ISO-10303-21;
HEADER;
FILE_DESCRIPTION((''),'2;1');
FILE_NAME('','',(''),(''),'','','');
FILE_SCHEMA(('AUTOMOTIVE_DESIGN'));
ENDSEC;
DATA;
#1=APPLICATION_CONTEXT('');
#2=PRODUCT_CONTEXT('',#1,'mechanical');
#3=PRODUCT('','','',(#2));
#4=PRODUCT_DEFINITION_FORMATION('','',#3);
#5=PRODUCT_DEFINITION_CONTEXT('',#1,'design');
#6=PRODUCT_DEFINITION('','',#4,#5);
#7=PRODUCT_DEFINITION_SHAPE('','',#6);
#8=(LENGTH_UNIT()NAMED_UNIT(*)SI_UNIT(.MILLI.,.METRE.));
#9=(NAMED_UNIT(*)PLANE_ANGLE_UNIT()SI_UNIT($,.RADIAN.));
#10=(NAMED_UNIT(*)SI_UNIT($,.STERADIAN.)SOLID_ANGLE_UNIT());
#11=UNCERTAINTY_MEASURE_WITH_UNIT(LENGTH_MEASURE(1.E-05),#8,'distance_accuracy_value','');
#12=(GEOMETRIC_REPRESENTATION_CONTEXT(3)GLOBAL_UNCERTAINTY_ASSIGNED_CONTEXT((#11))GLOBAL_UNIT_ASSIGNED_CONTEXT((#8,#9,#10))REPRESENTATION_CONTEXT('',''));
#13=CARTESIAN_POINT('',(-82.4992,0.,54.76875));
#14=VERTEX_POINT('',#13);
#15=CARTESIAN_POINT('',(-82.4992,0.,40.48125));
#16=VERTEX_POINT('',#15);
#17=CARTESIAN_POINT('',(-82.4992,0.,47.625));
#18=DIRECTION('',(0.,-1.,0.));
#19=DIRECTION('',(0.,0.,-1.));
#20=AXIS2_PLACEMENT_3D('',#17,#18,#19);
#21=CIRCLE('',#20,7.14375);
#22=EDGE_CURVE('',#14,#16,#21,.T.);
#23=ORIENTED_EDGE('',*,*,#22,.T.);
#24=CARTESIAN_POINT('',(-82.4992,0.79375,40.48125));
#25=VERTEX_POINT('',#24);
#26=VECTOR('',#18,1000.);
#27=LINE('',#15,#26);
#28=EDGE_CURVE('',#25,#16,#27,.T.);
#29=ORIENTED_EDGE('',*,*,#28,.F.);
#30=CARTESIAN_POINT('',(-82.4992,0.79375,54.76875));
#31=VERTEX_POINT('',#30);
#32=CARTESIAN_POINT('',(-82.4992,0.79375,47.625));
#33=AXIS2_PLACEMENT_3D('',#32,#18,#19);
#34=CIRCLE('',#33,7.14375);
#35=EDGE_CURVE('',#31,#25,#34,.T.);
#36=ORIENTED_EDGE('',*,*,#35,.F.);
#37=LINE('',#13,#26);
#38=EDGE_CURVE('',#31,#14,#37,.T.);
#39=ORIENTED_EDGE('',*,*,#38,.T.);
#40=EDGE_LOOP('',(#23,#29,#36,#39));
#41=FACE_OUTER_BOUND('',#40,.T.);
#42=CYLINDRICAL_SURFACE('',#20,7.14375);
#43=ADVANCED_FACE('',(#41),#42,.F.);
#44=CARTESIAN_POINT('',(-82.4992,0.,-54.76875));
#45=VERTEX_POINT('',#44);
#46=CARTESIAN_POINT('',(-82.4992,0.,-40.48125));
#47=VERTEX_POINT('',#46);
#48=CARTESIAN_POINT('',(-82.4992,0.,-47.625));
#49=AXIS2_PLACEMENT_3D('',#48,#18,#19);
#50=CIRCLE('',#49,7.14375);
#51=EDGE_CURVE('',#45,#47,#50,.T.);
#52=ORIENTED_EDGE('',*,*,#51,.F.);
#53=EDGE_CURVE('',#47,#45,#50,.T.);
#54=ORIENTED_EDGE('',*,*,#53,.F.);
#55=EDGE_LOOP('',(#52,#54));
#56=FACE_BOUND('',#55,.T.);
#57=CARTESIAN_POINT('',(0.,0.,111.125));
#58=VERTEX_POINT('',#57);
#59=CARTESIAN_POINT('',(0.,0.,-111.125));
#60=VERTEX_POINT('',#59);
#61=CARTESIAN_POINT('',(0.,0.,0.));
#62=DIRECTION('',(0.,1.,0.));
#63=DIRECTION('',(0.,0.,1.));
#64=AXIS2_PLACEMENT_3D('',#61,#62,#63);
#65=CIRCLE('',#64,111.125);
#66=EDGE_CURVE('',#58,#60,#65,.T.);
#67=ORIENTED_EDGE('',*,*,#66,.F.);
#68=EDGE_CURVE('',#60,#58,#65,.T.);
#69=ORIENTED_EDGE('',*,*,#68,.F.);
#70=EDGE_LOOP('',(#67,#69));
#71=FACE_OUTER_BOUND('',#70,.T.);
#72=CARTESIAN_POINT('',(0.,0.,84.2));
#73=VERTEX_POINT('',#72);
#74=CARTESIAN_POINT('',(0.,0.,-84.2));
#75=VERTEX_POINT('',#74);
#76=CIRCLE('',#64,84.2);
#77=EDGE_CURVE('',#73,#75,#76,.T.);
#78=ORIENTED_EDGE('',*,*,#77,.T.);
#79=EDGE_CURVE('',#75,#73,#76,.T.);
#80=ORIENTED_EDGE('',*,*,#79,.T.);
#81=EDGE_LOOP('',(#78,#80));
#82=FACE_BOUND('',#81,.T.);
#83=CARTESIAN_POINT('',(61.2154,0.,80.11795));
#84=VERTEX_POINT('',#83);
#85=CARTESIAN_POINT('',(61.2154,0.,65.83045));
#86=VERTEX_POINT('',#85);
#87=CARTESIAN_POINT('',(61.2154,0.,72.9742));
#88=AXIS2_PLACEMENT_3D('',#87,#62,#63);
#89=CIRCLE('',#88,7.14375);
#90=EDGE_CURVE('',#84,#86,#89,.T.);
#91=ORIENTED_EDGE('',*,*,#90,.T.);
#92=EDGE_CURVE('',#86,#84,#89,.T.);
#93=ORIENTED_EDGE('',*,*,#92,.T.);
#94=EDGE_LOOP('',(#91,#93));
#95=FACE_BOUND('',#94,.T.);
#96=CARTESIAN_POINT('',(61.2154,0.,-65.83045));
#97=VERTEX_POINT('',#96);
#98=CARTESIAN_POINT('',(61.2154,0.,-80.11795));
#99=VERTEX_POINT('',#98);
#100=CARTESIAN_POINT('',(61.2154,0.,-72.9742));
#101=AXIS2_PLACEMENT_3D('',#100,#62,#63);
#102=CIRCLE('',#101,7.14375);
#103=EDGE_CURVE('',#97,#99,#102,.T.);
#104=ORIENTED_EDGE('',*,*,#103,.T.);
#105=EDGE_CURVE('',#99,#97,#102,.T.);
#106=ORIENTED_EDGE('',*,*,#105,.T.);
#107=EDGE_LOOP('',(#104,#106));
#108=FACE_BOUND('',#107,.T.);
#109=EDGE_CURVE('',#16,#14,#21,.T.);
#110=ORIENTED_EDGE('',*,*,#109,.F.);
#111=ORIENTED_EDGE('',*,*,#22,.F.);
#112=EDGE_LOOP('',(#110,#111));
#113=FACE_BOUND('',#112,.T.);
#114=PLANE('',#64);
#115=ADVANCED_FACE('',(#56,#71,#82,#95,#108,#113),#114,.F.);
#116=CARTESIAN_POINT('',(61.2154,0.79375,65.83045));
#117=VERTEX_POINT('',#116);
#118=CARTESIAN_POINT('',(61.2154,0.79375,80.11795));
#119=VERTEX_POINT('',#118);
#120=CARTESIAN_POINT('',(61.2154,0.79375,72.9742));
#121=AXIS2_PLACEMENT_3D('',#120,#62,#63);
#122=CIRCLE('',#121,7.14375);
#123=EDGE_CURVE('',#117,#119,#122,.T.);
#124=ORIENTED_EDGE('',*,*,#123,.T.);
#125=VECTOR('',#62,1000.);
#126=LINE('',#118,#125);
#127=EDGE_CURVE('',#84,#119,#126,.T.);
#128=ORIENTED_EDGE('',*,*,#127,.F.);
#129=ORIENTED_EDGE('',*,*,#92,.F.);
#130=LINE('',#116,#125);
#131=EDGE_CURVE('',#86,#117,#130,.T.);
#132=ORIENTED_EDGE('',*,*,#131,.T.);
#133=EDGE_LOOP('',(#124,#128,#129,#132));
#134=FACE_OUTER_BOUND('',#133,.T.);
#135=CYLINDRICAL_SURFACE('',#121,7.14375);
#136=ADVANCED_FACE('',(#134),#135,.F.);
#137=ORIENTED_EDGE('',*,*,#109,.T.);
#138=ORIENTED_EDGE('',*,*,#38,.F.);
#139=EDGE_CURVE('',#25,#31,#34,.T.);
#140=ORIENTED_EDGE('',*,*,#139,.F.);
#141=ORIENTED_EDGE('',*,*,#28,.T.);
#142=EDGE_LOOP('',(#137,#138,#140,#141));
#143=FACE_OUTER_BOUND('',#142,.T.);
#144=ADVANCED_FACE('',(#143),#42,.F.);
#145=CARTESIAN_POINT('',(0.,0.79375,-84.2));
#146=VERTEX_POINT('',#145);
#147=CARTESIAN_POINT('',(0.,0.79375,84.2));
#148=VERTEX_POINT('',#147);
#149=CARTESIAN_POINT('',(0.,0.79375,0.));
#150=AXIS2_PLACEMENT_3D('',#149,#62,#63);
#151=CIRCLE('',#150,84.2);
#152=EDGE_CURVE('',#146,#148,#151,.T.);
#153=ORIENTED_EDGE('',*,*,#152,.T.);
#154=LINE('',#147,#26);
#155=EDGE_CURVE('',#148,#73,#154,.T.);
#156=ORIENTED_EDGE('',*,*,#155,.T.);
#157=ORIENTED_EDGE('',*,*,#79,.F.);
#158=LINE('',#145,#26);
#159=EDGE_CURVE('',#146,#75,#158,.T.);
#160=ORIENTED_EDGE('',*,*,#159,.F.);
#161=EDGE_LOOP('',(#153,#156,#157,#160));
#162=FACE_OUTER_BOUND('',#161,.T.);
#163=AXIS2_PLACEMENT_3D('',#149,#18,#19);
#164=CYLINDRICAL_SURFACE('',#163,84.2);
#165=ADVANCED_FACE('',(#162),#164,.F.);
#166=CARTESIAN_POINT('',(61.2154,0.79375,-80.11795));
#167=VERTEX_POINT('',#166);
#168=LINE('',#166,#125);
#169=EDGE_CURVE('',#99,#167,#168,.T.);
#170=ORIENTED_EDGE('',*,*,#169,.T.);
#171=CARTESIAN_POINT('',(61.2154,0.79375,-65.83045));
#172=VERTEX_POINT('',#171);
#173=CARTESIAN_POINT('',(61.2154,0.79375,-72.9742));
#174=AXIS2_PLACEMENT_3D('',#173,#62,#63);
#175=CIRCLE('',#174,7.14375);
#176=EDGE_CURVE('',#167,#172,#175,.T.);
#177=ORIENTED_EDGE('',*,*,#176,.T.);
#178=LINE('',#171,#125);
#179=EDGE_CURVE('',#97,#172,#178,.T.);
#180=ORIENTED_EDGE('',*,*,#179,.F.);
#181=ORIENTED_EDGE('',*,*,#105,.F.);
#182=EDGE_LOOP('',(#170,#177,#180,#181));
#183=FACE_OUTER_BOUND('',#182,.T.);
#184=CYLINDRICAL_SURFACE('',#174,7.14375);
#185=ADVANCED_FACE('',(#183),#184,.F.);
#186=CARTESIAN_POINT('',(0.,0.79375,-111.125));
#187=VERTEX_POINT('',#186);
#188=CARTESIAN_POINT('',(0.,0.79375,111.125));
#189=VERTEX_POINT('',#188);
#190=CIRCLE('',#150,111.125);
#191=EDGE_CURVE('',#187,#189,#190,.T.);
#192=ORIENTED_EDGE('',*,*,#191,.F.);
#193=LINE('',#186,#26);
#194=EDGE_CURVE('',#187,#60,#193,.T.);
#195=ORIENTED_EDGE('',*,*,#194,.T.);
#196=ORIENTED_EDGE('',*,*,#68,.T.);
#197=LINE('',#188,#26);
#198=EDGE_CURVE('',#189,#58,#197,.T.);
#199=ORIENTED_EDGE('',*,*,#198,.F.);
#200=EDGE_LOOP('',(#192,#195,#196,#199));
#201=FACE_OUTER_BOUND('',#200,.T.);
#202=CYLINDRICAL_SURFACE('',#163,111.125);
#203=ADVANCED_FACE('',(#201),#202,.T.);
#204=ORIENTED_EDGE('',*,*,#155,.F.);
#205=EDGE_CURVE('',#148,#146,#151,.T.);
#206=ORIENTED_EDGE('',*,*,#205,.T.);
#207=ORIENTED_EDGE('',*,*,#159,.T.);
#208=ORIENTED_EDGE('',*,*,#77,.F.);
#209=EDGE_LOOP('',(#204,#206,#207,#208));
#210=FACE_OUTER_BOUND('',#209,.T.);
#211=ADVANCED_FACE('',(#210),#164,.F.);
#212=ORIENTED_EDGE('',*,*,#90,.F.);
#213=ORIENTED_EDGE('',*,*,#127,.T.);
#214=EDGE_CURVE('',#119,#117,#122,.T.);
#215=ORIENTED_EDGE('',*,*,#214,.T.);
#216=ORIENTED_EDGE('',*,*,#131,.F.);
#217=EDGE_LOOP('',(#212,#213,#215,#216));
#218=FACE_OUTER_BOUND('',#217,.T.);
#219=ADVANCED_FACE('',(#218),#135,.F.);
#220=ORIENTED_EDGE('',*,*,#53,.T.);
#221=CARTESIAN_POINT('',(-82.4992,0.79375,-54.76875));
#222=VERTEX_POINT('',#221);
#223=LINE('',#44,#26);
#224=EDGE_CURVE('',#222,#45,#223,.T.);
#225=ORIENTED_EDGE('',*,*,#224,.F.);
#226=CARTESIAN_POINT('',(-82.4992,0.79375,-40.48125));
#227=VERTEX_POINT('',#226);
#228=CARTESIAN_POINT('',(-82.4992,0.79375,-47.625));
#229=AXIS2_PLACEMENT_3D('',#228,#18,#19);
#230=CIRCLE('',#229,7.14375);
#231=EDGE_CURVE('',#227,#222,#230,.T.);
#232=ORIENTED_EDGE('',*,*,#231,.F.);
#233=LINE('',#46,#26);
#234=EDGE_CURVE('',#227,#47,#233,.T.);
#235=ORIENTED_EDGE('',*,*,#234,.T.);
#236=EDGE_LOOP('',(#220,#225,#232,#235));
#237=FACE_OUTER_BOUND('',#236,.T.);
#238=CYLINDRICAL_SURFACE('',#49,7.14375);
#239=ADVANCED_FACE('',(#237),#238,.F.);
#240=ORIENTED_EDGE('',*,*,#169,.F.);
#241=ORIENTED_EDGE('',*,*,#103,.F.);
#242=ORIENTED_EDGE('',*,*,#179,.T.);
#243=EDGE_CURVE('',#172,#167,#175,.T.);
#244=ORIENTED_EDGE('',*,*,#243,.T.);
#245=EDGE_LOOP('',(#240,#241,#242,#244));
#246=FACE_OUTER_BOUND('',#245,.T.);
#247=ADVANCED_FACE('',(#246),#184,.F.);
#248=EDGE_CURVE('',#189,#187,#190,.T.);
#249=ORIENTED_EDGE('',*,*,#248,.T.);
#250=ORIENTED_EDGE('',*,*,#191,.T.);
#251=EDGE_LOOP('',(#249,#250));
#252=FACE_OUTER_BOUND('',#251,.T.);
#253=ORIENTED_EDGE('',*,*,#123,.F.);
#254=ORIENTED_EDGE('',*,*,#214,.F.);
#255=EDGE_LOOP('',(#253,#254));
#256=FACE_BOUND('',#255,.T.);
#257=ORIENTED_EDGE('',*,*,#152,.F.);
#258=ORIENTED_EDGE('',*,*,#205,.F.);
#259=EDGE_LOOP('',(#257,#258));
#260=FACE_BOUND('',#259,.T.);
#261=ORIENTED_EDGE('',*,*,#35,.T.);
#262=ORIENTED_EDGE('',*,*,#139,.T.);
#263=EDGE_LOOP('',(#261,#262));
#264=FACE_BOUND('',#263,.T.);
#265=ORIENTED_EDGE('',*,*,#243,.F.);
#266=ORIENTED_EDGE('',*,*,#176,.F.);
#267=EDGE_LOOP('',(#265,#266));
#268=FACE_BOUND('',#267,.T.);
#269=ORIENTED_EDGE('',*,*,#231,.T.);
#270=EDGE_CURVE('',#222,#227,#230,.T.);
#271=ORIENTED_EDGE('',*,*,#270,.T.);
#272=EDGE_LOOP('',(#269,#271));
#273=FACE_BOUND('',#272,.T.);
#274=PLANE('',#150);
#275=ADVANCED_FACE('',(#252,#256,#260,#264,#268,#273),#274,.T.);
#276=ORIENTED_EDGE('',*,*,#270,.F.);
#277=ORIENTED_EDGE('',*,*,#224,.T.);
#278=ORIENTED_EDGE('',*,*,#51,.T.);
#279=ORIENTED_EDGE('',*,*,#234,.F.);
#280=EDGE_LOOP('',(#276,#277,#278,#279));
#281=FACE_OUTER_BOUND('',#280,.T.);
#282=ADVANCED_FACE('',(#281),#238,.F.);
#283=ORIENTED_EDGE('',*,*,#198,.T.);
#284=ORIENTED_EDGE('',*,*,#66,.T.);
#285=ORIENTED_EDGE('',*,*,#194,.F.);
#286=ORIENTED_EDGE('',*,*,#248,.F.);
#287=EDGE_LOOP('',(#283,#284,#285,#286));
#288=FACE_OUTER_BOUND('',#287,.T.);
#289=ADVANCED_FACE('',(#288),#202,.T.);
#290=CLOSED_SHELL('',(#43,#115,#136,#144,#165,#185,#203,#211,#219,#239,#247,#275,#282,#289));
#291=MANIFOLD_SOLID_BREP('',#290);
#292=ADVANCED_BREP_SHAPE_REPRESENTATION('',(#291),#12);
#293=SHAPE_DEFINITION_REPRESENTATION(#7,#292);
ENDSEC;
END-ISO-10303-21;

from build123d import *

# Parameters (mm, degrees)
SKETCH1_R                      = 111.125
SKETCH1_R_2                    = 84.2
BOSS_EXTRUDE1_DEPTH            = 0.79375
F_9_16_0_5625_DIAMETER_HOLE1_D = 14.2875
F_9_16_0_5625_DIAMETER_HOLE2_D = 14.2875


with BuildPart() as part:
    # Sketch1 → Boss-Extrude1 (new body)
    with BuildSketch(Plane(origin=(0, 0, 0), x_dir=(1, 0, 0), z_dir=(0, 1, 0))):
        with Locations(Location((0, 0, 0), (0, 0, 270))):
            Circle(SKETCH1_R)
        with Locations(Location((0, 0, 0), (0, 0, 270))):
            Circle(SKETCH1_R_2, mode=Mode.SUBTRACT)
    extrude(amount=BOSS_EXTRUDE1_DEPTH)

    # 9/16 (0.5625) Diameter Hole1 (through all)
    with Locations(Plane(origin=(61.2154, 0.79375, -72.9742), x_dir=(0, 0, 1), z_dir=(0, 1, 0))):
        with Locations((0, 0)):
            f_9_16_0_5625_diameter_hole1 = Hole(F_9_16_0_5625_DIAMETER_HOLE1_D / 2)

    # 9/16 (0.5625) Diameter Hole2 (through all)
    with Locations(Plane(origin=(0, 0, 0), x_dir=(-1, 0, 0), z_dir=(0, -1, 0))):
        with Locations((82.4992, 47.625)):
            f_9_16_0_5625_diameter_hole2 = Hole(F_9_16_0_5625_DIAMETER_HOLE2_D / 2)

    # Mirror1: 9/16 (0.5625) Diameter Hole1, 9/16 (0.5625) Diameter Hole2 across plane
    add(f_9_16_0_5625_diameter_hole1.mirror(Plane.XY), mode=Mode.SUBTRACT)
    add(f_9_16_0_5625_diameter_hole2.mirror(Plane.XY), mode=Mode.SUBTRACT)


solid = part.part
